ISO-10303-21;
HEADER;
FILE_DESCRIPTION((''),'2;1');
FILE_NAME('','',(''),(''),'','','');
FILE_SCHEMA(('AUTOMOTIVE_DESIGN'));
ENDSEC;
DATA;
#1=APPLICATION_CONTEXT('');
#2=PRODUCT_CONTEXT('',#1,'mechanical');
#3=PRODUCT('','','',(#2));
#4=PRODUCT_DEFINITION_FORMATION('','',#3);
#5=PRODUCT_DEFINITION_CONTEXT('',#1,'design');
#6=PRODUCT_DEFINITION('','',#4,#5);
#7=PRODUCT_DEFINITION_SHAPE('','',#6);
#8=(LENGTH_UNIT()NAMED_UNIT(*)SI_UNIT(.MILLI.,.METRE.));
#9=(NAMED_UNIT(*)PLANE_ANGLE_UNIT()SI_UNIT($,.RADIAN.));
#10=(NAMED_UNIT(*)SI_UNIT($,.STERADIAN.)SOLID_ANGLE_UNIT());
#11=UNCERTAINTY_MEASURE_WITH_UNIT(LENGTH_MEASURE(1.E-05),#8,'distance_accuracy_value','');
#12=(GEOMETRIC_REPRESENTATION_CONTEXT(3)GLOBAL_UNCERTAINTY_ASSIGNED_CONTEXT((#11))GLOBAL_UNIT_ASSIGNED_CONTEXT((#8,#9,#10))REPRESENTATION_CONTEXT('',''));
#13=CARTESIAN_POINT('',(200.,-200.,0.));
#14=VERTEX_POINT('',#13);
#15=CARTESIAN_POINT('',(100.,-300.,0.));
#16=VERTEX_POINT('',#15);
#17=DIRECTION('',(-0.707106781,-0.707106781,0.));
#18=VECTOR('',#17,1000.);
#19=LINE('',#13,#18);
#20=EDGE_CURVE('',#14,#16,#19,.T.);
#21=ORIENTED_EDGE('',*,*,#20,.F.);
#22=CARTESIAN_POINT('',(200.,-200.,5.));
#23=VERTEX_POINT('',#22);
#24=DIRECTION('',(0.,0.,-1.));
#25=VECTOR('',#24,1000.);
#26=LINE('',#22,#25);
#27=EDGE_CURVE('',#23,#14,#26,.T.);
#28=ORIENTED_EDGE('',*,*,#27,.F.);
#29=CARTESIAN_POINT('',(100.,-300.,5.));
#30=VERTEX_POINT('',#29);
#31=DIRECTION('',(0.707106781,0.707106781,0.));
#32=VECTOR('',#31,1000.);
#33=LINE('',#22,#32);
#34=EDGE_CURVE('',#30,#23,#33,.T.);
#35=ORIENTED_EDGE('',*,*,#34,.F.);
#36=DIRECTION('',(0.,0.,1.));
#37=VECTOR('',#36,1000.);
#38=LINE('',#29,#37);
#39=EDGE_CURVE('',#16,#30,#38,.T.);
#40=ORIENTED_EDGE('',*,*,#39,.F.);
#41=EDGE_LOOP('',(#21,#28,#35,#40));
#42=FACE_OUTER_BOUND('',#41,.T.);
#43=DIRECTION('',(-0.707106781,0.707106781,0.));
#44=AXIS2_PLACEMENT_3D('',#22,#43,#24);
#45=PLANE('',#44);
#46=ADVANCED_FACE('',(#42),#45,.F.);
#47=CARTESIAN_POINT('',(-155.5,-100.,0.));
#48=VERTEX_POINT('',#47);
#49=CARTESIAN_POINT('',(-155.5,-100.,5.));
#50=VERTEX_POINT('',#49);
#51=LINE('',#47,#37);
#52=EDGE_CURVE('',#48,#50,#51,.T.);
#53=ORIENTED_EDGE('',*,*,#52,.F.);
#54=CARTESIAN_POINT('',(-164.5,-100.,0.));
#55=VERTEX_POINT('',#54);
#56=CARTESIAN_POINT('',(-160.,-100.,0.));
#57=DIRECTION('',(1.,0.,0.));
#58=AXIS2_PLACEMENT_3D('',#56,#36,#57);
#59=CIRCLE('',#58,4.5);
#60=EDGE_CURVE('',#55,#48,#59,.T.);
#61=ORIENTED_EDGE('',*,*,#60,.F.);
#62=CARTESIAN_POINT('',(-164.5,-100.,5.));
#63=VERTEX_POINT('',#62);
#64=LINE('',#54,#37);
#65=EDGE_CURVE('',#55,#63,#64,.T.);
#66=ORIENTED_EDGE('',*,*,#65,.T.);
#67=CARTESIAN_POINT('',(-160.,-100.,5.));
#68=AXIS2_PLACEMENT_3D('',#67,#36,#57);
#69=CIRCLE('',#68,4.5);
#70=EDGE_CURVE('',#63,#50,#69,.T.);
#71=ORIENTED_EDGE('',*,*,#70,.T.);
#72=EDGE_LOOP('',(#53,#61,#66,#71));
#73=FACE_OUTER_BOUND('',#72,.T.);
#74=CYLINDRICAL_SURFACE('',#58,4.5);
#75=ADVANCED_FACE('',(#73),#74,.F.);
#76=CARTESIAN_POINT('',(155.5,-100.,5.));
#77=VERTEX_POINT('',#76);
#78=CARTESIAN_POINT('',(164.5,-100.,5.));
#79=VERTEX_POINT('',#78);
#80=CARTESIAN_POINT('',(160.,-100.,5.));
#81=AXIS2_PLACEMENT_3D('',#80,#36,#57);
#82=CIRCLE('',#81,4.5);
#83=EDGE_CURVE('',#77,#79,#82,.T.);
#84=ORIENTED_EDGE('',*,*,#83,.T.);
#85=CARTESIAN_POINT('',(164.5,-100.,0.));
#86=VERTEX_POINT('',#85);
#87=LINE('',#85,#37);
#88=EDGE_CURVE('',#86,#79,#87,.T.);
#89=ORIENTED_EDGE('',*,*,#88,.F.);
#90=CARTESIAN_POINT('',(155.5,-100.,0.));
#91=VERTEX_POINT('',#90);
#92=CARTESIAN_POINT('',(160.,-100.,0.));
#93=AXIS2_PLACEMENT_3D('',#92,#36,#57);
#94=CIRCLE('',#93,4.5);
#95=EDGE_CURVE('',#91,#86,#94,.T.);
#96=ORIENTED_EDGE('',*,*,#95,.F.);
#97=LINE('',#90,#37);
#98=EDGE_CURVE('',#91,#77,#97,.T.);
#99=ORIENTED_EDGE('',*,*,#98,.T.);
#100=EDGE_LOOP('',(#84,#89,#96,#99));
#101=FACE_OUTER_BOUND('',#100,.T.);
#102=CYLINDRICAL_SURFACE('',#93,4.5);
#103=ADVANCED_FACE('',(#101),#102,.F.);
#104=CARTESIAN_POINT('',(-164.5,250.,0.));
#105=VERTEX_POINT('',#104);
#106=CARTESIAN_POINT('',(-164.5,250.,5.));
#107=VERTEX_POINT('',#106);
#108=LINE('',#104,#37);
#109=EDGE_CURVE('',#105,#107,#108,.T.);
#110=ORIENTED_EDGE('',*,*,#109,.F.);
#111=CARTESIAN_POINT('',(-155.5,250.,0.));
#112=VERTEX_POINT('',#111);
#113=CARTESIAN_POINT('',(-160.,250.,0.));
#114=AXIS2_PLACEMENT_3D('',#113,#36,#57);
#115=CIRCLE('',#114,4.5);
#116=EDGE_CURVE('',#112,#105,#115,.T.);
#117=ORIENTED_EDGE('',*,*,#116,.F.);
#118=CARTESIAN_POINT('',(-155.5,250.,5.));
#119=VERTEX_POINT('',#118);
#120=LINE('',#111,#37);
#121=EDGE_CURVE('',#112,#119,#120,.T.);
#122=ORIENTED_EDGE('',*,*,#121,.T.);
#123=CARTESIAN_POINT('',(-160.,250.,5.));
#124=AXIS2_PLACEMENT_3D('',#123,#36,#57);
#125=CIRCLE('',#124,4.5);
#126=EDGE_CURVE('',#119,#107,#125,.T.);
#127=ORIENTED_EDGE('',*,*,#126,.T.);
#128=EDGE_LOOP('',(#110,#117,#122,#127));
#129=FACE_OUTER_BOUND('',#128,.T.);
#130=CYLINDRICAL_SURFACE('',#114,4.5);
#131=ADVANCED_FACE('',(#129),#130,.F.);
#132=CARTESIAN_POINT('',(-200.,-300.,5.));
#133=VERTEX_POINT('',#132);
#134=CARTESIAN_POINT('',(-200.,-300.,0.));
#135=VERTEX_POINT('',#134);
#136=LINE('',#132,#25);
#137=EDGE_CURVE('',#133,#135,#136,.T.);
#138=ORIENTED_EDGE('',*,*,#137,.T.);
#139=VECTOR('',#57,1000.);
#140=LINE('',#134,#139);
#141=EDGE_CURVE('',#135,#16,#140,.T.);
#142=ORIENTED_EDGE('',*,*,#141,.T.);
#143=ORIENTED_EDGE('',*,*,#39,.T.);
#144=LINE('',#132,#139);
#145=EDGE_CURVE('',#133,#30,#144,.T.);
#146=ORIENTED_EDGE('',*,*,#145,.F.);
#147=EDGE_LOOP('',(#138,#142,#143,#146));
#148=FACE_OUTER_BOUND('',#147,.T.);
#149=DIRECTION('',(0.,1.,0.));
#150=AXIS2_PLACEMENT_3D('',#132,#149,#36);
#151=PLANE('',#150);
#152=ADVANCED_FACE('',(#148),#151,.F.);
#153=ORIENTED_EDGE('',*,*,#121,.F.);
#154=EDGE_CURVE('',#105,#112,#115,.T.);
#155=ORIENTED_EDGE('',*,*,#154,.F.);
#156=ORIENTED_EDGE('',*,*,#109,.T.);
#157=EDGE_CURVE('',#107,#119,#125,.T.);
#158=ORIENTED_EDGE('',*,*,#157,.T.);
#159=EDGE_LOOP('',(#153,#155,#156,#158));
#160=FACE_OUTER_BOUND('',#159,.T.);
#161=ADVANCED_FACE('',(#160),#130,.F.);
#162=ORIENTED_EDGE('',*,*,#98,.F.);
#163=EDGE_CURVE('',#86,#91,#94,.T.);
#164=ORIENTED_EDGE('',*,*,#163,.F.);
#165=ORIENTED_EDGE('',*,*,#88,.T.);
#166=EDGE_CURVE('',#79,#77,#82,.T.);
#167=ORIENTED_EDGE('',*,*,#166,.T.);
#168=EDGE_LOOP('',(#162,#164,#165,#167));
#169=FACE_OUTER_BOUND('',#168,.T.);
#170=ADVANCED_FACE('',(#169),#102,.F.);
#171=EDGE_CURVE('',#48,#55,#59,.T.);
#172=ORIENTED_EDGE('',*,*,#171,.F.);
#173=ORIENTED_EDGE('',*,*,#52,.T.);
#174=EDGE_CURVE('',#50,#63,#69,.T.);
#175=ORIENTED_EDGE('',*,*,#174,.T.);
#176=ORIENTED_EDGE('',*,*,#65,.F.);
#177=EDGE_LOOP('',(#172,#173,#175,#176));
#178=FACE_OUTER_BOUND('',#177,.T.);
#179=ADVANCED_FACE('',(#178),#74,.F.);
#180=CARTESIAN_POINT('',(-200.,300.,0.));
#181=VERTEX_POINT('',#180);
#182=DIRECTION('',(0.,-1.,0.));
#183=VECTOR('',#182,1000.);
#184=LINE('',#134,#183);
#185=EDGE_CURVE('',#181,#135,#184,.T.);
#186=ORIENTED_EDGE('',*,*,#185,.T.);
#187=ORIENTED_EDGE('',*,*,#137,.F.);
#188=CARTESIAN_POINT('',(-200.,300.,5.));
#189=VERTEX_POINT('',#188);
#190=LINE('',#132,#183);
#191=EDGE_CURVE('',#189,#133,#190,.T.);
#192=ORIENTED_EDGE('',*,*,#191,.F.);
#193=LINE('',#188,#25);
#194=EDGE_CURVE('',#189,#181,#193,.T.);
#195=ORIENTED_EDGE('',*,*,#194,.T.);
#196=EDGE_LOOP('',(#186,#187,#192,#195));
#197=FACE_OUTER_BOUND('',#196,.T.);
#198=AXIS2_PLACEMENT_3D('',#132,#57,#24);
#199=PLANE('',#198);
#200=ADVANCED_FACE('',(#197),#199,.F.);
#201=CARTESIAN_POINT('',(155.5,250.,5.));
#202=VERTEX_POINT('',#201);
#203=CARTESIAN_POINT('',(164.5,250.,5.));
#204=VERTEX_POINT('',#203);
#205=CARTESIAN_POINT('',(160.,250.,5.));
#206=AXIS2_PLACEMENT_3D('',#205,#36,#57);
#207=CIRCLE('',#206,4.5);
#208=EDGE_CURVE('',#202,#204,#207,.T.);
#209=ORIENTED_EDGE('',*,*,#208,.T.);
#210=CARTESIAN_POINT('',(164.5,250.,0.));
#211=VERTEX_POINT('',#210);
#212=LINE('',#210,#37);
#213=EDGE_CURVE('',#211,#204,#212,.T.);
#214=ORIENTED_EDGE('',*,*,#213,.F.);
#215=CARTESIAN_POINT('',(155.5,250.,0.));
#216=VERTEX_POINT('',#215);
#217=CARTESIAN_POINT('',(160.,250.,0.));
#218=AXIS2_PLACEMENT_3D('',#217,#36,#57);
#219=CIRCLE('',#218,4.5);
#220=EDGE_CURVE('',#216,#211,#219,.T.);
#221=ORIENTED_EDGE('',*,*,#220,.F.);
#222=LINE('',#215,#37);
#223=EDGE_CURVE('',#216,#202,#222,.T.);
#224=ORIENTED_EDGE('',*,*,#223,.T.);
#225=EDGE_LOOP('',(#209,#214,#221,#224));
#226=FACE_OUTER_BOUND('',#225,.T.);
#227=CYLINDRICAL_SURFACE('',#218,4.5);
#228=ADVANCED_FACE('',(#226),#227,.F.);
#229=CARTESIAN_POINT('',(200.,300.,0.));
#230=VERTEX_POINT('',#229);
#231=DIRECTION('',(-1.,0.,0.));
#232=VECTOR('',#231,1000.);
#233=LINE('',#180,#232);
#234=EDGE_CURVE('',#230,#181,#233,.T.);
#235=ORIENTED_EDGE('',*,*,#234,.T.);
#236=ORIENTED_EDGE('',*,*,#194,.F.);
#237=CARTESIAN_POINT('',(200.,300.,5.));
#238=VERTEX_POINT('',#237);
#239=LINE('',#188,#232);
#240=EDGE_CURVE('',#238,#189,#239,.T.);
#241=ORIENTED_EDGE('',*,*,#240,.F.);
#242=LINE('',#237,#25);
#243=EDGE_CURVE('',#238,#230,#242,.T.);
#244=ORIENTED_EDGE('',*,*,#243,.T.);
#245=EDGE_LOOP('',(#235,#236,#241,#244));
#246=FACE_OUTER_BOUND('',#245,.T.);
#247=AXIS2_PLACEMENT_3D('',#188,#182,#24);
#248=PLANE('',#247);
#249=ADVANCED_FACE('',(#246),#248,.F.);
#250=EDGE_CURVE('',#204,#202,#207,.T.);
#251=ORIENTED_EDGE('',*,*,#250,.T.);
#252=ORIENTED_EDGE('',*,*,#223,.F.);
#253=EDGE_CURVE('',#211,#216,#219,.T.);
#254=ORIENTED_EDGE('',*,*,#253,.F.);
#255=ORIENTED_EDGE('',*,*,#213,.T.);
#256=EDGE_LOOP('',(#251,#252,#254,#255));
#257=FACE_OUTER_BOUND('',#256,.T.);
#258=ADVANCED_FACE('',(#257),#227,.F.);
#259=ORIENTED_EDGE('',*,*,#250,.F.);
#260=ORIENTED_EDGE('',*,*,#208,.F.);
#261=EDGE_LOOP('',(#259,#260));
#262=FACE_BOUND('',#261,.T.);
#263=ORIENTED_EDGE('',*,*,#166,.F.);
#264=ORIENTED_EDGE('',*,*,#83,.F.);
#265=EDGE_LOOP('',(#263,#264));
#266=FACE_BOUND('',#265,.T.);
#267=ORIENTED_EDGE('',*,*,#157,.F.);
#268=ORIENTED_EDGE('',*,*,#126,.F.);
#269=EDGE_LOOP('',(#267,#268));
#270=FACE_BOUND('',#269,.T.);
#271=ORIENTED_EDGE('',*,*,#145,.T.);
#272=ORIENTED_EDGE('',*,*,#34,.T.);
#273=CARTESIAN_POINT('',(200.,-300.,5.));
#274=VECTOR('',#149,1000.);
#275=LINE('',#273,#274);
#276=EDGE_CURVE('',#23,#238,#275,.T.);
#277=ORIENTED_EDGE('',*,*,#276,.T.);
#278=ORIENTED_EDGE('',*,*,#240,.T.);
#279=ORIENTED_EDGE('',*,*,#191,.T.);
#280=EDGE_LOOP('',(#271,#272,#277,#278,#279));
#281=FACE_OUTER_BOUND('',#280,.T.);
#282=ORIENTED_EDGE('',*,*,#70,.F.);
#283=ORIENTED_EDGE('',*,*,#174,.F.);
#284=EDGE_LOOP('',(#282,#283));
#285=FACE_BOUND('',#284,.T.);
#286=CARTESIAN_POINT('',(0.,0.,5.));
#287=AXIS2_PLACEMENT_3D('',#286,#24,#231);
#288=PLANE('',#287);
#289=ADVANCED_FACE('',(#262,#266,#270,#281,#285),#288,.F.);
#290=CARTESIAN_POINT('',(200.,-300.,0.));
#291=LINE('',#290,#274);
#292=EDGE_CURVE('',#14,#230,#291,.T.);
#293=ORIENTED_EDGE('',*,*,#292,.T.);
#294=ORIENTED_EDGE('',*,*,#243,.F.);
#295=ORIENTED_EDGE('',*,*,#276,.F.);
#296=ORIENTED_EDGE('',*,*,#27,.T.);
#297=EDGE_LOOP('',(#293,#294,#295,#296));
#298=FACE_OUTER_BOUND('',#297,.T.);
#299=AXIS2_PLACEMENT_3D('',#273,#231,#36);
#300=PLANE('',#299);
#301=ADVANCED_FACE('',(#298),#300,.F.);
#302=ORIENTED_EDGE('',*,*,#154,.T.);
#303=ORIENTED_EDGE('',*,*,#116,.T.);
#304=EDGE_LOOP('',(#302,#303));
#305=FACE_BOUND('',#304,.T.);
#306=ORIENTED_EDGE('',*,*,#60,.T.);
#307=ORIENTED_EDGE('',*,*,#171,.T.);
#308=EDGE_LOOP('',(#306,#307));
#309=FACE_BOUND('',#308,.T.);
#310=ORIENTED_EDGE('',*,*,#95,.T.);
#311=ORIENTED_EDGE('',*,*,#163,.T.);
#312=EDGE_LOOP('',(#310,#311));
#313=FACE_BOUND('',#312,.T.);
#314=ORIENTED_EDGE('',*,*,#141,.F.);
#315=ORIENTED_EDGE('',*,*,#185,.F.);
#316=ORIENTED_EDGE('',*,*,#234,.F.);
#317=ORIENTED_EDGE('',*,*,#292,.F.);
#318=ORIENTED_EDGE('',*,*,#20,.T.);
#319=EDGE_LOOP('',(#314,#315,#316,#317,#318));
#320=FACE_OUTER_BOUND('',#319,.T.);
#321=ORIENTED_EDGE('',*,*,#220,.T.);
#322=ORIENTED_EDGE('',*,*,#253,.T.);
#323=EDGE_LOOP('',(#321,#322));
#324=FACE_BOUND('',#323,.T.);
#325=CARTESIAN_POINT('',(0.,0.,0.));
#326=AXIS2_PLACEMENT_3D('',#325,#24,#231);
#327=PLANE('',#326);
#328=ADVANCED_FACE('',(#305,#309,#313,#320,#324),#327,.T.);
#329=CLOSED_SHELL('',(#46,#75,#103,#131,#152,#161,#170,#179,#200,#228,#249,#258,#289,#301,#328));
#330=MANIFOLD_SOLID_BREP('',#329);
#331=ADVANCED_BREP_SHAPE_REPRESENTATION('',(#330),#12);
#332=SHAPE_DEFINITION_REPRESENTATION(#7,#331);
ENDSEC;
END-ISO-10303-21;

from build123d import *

# Parameters (mm, degrees)
SKETCH_1_W          = 400
SKETCH_1_H          = 600
EXTRUDE_1_DEPTH     = 5
SKETCH_2_R          = 4.5
CUT_EXTRUDE_1_DEPTH = 361.589794642
CHAMFER_1_SIZE      = 100


with BuildPart() as part:
    # 草图1 → 凸台-拉伸1 (new body)
    with BuildSketch(Plane.XY):
        Rectangle(SKETCH_1_W, SKETCH_1_H)
    extrude(amount=EXTRUDE_1_DEPTH)

    # 草图2 → 切除-拉伸1 (cut, through all)
    with BuildSketch(Plane.XY.offset(5)):
        with Locations((-160, 250)):
            Circle(SKETCH_2_R)
        with Locations((160, 250)):
            Circle(SKETCH_2_R)
        with Locations((160, -100)):
            Circle(SKETCH_2_R)
        with Locations((-160, -100)):
            Circle(SKETCH_2_R)
    extrude(amount=-CUT_EXTRUDE_1_DEPTH, mode=Mode.SUBTRACT)

    # 倒角1
    chamfer_1_edges = [part.edges().sort_by_distance(p)[0] for p in [
        (200, -300, 2.5),
    ]]
    chamfer(chamfer_1_edges, length=CHAMFER_1_SIZE)


solid = part.part
